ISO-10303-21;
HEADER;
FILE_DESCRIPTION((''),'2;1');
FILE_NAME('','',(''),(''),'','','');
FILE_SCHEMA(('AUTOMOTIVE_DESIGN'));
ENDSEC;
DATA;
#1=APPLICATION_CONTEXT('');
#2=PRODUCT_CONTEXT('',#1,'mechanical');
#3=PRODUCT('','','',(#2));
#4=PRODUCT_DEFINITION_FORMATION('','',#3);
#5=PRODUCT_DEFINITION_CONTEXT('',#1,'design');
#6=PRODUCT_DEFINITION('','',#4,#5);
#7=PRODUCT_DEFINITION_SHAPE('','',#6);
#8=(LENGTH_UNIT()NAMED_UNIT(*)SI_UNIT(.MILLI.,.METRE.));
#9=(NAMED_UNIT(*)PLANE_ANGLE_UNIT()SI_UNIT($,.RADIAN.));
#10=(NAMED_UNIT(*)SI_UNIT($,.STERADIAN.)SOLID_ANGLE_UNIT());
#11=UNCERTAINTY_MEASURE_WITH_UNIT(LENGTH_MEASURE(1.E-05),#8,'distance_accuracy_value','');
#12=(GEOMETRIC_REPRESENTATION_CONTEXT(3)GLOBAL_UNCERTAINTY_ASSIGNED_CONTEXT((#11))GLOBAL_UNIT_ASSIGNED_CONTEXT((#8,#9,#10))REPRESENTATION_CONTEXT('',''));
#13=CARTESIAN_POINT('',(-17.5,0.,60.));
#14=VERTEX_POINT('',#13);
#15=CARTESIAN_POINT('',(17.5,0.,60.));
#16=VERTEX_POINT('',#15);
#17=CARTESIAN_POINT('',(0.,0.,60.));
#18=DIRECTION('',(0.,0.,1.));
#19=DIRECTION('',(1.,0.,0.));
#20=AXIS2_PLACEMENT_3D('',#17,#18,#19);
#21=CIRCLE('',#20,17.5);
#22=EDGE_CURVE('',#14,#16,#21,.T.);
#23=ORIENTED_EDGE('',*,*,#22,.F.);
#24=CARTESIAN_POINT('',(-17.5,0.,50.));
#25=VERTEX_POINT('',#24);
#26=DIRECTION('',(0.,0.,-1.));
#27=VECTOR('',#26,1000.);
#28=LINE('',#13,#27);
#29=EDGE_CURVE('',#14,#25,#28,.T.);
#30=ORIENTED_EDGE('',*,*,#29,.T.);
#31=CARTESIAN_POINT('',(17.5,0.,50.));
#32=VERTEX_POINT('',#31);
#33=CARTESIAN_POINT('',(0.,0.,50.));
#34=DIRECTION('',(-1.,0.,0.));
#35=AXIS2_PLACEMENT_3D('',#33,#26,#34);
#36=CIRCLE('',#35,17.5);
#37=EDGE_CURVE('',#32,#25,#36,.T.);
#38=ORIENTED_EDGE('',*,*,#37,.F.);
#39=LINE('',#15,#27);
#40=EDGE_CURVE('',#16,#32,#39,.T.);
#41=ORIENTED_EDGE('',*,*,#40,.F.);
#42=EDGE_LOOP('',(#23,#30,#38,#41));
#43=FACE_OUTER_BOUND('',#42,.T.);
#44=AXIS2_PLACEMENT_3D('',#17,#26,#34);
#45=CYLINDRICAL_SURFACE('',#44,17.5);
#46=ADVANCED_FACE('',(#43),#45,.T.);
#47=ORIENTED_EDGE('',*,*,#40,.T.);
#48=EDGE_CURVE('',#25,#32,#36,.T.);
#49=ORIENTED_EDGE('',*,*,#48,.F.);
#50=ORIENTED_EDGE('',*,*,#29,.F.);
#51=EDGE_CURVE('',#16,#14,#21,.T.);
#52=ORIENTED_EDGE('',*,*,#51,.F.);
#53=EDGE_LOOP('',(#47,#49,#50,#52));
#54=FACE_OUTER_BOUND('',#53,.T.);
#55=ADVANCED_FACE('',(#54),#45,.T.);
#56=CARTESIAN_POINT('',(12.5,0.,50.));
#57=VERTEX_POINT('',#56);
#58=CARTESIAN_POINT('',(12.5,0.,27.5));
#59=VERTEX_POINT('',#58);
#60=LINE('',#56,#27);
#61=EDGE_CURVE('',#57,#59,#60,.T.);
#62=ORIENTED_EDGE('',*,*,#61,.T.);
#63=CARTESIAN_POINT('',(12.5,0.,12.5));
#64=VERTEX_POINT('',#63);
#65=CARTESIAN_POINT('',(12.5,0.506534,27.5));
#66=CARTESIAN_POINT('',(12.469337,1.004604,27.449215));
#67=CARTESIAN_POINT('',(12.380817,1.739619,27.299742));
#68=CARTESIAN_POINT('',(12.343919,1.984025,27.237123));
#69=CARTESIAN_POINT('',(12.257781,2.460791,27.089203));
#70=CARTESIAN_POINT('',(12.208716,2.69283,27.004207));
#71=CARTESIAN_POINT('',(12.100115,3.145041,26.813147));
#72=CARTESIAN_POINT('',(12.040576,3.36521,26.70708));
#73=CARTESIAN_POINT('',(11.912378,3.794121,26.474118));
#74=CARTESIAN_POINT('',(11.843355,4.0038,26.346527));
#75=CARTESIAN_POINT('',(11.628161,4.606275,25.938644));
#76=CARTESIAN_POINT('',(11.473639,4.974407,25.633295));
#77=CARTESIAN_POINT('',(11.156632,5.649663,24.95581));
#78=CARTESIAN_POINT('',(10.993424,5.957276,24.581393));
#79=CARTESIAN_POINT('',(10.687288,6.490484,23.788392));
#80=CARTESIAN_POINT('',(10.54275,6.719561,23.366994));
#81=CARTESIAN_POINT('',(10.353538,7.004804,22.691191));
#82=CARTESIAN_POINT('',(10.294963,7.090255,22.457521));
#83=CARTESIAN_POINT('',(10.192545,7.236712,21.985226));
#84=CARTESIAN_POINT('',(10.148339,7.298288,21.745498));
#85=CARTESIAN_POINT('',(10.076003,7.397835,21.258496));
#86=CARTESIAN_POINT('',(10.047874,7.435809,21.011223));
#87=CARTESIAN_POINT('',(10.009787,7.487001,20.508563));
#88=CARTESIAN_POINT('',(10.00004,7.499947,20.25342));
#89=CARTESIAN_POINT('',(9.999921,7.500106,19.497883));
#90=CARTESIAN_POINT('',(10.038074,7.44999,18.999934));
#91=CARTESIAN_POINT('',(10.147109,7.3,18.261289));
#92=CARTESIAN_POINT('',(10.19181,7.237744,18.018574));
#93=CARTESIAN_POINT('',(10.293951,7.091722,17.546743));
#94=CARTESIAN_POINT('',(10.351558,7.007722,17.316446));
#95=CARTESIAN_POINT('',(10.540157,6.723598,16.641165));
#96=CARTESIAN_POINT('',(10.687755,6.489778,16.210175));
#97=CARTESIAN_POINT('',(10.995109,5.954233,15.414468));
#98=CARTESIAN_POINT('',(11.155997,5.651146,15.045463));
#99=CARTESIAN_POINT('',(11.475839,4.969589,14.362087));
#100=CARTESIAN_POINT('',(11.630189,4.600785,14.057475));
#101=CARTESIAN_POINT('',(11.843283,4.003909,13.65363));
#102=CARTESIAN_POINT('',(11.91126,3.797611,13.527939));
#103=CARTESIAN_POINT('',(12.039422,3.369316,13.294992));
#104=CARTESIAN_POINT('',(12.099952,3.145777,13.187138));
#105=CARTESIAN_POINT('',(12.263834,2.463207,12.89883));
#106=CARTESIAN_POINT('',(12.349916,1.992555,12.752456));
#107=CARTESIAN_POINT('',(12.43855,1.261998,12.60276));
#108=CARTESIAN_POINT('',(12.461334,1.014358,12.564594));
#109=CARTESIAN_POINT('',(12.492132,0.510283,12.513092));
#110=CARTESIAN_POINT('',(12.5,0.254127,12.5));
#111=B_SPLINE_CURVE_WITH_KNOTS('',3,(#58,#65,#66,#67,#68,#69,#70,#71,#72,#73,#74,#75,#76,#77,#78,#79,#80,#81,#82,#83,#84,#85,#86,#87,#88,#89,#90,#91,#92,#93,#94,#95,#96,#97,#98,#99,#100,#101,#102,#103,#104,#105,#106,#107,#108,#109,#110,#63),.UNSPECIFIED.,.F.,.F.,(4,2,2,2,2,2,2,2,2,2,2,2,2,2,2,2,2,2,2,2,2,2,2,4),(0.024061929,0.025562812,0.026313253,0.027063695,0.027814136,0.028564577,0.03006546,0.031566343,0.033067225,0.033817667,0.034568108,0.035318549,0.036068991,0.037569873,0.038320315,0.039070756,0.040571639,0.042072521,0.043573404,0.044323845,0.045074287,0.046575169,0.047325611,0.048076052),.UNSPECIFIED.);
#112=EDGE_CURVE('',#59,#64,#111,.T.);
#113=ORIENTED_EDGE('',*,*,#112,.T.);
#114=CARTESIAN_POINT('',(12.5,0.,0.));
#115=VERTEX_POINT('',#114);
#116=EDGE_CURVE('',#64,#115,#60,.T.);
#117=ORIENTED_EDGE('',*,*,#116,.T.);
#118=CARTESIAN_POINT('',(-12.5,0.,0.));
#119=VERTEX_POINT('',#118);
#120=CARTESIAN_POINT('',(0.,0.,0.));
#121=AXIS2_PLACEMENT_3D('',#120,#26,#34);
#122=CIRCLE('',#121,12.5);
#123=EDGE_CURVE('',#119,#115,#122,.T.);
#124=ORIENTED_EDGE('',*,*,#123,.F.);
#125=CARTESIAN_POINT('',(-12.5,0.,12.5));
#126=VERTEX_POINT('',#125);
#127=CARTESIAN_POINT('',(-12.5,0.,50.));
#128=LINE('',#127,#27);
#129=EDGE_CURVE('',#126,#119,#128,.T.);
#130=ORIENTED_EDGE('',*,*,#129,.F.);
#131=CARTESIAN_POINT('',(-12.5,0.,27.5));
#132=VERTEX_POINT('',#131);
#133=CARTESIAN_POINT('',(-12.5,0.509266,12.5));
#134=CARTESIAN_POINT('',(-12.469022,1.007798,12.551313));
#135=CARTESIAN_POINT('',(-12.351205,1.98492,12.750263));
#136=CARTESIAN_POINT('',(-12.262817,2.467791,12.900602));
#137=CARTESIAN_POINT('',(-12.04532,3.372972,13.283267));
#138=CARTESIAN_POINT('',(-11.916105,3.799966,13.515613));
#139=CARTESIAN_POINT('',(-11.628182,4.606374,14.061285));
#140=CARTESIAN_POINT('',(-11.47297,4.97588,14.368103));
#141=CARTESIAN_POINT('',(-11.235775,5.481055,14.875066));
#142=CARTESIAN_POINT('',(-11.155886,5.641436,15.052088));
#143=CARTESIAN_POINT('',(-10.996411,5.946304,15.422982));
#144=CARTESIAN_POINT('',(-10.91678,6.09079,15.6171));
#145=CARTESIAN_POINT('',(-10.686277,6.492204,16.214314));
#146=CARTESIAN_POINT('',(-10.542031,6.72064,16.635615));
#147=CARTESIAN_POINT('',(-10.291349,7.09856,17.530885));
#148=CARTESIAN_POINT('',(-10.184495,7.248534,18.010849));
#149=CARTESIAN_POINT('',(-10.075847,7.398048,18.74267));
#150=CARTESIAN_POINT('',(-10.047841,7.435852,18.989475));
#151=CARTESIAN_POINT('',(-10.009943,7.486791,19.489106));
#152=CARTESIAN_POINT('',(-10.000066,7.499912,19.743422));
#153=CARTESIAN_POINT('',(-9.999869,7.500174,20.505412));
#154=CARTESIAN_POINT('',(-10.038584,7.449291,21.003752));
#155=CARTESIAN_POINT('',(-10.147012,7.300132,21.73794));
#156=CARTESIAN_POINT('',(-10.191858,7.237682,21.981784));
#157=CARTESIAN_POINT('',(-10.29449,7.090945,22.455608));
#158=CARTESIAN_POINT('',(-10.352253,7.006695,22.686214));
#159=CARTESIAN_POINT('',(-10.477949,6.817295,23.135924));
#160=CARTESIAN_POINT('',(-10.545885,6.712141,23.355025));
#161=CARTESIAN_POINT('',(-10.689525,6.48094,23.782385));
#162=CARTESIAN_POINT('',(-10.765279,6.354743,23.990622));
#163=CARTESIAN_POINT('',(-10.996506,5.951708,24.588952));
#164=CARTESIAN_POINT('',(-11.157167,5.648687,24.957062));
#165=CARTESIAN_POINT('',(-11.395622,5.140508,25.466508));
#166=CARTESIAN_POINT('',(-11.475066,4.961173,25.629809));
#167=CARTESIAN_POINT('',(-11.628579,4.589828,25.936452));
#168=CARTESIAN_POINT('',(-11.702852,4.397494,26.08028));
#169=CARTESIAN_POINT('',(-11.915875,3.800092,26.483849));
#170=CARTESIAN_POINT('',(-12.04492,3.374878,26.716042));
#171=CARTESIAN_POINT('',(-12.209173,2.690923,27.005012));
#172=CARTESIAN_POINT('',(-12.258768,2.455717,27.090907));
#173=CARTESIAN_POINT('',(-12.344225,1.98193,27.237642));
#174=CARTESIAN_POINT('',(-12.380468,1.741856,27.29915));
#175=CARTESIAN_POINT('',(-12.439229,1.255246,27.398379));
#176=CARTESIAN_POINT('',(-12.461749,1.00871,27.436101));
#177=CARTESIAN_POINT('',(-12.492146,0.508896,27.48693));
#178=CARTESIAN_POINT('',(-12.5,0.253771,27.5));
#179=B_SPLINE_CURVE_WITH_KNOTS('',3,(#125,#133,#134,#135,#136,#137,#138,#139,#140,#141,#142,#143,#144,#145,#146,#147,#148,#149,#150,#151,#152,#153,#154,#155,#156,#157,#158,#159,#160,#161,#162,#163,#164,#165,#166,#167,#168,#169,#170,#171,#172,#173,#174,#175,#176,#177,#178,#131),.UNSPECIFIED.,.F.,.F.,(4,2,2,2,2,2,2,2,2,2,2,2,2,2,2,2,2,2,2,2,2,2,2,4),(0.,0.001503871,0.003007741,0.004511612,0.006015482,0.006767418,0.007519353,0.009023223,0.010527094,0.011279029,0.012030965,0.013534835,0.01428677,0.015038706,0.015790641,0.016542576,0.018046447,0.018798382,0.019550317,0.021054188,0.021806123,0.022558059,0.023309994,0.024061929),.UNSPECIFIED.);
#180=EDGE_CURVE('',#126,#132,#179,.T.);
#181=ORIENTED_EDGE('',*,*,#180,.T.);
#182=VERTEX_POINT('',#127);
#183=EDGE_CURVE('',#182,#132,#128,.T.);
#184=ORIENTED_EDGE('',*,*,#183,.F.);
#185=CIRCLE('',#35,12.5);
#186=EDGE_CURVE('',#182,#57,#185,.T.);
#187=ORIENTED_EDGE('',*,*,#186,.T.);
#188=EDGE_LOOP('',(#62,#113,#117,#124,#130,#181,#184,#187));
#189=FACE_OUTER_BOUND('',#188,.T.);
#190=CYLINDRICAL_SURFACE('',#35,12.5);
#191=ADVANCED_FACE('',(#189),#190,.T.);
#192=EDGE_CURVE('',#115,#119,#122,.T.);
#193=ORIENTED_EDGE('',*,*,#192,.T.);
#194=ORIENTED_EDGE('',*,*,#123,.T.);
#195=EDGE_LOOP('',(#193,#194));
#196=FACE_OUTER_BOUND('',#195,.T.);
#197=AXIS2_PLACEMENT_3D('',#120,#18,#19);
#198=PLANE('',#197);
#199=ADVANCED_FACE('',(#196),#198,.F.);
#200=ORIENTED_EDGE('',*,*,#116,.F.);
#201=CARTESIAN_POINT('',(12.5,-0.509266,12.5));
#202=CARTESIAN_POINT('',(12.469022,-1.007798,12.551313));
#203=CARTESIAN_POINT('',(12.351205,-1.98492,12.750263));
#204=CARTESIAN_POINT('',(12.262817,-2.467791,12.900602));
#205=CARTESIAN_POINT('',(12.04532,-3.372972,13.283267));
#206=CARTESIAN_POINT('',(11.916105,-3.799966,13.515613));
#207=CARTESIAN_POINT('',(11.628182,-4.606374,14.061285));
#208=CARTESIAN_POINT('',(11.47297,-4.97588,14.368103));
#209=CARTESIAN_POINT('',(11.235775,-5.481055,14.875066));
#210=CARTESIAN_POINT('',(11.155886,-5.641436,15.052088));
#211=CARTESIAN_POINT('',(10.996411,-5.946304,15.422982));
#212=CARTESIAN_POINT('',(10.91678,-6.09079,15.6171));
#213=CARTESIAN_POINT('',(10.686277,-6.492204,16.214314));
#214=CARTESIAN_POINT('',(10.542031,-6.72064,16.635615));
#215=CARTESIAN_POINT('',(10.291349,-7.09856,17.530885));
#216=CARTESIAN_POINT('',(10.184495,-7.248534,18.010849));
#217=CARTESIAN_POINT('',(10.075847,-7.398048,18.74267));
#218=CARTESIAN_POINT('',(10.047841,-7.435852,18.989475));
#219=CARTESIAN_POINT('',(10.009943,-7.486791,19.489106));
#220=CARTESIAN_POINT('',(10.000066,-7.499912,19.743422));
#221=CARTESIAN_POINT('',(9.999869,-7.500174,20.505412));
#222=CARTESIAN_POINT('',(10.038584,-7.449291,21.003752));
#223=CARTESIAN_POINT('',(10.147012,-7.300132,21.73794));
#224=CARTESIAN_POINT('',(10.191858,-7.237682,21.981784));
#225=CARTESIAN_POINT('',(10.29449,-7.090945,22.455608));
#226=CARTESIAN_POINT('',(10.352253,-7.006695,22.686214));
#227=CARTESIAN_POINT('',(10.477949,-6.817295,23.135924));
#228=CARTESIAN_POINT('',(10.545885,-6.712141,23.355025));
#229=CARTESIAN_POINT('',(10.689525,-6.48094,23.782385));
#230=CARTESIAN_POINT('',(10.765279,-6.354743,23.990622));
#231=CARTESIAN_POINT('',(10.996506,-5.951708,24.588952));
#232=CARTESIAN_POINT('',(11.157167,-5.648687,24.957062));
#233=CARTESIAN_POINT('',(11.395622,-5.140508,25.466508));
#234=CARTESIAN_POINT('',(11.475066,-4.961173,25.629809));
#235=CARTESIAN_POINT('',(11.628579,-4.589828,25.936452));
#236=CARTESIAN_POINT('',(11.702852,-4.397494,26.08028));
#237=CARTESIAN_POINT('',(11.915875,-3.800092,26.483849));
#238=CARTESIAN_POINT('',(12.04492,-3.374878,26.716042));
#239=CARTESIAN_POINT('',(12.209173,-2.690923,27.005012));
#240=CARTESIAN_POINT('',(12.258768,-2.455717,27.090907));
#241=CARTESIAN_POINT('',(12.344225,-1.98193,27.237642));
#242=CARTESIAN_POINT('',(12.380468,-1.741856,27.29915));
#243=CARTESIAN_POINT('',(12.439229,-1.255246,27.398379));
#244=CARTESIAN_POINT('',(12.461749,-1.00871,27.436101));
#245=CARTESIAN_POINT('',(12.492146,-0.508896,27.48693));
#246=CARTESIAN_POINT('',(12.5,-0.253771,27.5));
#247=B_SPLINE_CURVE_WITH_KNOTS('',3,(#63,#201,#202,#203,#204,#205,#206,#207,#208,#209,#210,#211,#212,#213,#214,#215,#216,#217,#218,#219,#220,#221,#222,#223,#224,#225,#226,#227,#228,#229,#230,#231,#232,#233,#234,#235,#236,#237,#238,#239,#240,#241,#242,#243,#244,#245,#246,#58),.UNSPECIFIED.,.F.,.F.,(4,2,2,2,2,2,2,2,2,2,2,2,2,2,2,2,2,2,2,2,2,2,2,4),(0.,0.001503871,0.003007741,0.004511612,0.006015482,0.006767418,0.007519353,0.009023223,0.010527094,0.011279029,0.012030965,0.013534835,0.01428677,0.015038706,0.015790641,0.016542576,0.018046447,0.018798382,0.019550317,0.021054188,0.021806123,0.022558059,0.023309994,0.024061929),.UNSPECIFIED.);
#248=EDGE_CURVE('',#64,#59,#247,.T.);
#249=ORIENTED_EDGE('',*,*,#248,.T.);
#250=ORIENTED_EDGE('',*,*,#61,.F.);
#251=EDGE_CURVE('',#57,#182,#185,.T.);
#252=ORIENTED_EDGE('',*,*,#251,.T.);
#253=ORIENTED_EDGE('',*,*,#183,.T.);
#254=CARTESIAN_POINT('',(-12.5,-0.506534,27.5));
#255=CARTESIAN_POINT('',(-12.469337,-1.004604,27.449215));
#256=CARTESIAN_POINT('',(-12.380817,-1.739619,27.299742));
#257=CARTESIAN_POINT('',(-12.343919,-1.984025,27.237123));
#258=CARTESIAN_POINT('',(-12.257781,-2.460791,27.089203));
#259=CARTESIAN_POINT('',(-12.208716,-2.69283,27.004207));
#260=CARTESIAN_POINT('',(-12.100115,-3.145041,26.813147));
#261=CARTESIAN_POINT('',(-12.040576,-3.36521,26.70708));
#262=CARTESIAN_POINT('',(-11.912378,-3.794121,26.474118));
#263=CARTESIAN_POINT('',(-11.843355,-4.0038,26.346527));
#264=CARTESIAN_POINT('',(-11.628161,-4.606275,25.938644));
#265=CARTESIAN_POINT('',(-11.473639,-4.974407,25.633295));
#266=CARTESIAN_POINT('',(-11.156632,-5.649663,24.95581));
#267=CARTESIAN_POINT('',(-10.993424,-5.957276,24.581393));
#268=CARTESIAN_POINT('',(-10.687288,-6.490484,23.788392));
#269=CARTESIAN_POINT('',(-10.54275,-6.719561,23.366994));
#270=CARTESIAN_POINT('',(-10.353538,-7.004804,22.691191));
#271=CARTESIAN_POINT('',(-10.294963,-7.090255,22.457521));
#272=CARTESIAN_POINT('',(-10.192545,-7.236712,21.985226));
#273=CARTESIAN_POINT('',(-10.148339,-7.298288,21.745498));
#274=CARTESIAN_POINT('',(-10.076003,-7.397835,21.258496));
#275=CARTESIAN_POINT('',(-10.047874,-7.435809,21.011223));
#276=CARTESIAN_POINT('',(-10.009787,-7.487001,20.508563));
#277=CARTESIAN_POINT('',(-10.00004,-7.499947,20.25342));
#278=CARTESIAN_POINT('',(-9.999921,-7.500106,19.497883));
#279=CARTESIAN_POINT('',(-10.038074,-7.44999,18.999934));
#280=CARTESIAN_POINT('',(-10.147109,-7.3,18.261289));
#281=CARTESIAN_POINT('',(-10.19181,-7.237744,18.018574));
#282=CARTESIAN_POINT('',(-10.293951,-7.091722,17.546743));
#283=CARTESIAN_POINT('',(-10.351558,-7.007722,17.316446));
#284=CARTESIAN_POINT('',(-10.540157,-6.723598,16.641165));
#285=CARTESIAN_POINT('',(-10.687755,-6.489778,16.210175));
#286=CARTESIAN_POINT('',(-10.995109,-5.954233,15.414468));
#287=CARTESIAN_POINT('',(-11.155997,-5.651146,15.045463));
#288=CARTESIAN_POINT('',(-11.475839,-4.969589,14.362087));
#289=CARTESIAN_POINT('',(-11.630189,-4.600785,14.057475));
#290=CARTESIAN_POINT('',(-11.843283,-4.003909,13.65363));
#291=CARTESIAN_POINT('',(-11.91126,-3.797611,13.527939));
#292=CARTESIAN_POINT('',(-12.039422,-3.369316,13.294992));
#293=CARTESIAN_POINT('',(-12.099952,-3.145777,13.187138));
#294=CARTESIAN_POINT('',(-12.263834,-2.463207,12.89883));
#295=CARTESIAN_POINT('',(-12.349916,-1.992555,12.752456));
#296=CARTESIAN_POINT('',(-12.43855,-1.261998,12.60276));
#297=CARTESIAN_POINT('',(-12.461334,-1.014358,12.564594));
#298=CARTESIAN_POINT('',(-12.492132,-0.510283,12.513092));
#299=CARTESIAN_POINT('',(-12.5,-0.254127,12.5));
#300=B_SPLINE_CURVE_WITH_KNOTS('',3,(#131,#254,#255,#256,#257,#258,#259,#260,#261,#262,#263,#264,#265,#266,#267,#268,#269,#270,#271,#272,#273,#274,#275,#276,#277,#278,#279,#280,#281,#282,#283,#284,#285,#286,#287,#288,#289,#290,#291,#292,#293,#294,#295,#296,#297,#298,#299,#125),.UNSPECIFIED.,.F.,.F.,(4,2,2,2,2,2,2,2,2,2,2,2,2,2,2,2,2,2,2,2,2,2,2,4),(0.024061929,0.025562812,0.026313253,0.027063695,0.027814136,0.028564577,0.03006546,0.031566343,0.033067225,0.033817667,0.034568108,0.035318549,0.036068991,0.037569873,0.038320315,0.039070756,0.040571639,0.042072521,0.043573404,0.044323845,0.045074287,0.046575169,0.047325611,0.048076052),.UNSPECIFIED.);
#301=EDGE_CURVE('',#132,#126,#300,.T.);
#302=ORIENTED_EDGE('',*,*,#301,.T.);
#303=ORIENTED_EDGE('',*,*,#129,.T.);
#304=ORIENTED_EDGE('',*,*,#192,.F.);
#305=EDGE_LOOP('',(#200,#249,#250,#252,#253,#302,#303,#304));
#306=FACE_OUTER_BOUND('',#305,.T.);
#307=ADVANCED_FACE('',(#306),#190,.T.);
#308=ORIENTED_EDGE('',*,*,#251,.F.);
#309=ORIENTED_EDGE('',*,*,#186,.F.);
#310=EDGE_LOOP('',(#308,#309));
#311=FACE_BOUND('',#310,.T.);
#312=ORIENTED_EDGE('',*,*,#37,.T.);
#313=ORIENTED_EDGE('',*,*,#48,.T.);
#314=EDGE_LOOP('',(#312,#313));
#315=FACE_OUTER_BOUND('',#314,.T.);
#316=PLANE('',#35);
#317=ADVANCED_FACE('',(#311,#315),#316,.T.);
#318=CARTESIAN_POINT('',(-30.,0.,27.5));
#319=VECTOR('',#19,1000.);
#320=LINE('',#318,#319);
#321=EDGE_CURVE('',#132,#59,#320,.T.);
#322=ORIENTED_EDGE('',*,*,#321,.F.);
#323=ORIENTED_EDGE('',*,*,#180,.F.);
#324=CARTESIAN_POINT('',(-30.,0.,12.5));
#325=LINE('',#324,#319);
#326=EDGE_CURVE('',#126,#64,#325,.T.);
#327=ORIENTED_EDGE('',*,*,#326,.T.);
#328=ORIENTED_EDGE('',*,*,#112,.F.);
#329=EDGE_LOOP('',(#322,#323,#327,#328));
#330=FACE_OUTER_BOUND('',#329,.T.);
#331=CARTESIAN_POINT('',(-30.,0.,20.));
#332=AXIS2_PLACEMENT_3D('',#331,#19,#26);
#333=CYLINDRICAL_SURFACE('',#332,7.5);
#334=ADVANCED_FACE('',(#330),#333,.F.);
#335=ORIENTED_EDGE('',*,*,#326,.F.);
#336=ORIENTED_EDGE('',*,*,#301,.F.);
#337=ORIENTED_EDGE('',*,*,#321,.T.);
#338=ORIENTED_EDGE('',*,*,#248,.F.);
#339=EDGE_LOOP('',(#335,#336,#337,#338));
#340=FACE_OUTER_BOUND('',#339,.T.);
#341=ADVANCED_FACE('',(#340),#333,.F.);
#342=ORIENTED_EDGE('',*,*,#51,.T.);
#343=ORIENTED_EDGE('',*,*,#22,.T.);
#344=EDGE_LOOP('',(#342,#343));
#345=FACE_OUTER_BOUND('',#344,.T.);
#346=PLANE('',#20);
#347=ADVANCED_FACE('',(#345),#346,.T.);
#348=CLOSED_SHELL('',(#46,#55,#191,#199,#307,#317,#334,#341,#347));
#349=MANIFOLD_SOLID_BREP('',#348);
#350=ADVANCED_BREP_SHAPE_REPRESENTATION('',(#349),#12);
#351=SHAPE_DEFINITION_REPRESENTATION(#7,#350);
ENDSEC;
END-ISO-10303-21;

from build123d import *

# Parameters (mm, degrees)
SKETCH1_R           = 17.5
BOSS_EXTRUDE1_DEPTH = 60
CHAMFER1_SIZE       = 1
SKETCH2_R           = 7.5
CUT_EXTRUDE1_DEPTH  = 30
SKETCH3_OUTSIDE_W   = 52.556
SKETCH3_OUTSIDE_H   = 52.556
SKETCH3_OUTSIDE_R   = 12.5
CUT_EXTRUDE2_DEPTH  = 50


with BuildPart() as part:
    # Sketch1 → Boss-Extrude1 (new body)
    with BuildSketch(Plane.XY):
        Circle(SKETCH1_R)
    extrude(amount=BOSS_EXTRUDE1_DEPTH)

    # Chamfer1
    chamfer1_edges = [part.edges().sort_by_distance(p)[0] for p in [
        (-17.5, 0, 0),
    ]]
    chamfer(chamfer1_edges, length=CHAMFER1_SIZE)

    # Sketch2 → Cut-Extrude1 (cut, symmetric)
    with BuildSketch(Plane(origin=(0, 0, 0), x_dir=(0, 0, -1), z_dir=(1, 0, 0))):
        with Locations(Location((-20, 0, 0), (0, 0, 180))):
            Circle(SKETCH2_R)
    extrude(amount=CUT_EXTRUDE1_DEPTH, both=True, mode=Mode.SUBTRACT)

    # Sketch3 outside → Cut-Extrude2 (cut)
    with BuildSketch(Plane(origin=(0, 0, 0), x_dir=(-1, 0, 0), z_dir=(0, 0, -1))):
        Rectangle(SKETCH3_OUTSIDE_W, SKETCH3_OUTSIDE_H)
        Circle(SKETCH3_OUTSIDE_R, mode=Mode.SUBTRACT)
    extrude(amount=-CUT_EXTRUDE2_DEPTH, mode=Mode.SUBTRACT)


solid = part.part
